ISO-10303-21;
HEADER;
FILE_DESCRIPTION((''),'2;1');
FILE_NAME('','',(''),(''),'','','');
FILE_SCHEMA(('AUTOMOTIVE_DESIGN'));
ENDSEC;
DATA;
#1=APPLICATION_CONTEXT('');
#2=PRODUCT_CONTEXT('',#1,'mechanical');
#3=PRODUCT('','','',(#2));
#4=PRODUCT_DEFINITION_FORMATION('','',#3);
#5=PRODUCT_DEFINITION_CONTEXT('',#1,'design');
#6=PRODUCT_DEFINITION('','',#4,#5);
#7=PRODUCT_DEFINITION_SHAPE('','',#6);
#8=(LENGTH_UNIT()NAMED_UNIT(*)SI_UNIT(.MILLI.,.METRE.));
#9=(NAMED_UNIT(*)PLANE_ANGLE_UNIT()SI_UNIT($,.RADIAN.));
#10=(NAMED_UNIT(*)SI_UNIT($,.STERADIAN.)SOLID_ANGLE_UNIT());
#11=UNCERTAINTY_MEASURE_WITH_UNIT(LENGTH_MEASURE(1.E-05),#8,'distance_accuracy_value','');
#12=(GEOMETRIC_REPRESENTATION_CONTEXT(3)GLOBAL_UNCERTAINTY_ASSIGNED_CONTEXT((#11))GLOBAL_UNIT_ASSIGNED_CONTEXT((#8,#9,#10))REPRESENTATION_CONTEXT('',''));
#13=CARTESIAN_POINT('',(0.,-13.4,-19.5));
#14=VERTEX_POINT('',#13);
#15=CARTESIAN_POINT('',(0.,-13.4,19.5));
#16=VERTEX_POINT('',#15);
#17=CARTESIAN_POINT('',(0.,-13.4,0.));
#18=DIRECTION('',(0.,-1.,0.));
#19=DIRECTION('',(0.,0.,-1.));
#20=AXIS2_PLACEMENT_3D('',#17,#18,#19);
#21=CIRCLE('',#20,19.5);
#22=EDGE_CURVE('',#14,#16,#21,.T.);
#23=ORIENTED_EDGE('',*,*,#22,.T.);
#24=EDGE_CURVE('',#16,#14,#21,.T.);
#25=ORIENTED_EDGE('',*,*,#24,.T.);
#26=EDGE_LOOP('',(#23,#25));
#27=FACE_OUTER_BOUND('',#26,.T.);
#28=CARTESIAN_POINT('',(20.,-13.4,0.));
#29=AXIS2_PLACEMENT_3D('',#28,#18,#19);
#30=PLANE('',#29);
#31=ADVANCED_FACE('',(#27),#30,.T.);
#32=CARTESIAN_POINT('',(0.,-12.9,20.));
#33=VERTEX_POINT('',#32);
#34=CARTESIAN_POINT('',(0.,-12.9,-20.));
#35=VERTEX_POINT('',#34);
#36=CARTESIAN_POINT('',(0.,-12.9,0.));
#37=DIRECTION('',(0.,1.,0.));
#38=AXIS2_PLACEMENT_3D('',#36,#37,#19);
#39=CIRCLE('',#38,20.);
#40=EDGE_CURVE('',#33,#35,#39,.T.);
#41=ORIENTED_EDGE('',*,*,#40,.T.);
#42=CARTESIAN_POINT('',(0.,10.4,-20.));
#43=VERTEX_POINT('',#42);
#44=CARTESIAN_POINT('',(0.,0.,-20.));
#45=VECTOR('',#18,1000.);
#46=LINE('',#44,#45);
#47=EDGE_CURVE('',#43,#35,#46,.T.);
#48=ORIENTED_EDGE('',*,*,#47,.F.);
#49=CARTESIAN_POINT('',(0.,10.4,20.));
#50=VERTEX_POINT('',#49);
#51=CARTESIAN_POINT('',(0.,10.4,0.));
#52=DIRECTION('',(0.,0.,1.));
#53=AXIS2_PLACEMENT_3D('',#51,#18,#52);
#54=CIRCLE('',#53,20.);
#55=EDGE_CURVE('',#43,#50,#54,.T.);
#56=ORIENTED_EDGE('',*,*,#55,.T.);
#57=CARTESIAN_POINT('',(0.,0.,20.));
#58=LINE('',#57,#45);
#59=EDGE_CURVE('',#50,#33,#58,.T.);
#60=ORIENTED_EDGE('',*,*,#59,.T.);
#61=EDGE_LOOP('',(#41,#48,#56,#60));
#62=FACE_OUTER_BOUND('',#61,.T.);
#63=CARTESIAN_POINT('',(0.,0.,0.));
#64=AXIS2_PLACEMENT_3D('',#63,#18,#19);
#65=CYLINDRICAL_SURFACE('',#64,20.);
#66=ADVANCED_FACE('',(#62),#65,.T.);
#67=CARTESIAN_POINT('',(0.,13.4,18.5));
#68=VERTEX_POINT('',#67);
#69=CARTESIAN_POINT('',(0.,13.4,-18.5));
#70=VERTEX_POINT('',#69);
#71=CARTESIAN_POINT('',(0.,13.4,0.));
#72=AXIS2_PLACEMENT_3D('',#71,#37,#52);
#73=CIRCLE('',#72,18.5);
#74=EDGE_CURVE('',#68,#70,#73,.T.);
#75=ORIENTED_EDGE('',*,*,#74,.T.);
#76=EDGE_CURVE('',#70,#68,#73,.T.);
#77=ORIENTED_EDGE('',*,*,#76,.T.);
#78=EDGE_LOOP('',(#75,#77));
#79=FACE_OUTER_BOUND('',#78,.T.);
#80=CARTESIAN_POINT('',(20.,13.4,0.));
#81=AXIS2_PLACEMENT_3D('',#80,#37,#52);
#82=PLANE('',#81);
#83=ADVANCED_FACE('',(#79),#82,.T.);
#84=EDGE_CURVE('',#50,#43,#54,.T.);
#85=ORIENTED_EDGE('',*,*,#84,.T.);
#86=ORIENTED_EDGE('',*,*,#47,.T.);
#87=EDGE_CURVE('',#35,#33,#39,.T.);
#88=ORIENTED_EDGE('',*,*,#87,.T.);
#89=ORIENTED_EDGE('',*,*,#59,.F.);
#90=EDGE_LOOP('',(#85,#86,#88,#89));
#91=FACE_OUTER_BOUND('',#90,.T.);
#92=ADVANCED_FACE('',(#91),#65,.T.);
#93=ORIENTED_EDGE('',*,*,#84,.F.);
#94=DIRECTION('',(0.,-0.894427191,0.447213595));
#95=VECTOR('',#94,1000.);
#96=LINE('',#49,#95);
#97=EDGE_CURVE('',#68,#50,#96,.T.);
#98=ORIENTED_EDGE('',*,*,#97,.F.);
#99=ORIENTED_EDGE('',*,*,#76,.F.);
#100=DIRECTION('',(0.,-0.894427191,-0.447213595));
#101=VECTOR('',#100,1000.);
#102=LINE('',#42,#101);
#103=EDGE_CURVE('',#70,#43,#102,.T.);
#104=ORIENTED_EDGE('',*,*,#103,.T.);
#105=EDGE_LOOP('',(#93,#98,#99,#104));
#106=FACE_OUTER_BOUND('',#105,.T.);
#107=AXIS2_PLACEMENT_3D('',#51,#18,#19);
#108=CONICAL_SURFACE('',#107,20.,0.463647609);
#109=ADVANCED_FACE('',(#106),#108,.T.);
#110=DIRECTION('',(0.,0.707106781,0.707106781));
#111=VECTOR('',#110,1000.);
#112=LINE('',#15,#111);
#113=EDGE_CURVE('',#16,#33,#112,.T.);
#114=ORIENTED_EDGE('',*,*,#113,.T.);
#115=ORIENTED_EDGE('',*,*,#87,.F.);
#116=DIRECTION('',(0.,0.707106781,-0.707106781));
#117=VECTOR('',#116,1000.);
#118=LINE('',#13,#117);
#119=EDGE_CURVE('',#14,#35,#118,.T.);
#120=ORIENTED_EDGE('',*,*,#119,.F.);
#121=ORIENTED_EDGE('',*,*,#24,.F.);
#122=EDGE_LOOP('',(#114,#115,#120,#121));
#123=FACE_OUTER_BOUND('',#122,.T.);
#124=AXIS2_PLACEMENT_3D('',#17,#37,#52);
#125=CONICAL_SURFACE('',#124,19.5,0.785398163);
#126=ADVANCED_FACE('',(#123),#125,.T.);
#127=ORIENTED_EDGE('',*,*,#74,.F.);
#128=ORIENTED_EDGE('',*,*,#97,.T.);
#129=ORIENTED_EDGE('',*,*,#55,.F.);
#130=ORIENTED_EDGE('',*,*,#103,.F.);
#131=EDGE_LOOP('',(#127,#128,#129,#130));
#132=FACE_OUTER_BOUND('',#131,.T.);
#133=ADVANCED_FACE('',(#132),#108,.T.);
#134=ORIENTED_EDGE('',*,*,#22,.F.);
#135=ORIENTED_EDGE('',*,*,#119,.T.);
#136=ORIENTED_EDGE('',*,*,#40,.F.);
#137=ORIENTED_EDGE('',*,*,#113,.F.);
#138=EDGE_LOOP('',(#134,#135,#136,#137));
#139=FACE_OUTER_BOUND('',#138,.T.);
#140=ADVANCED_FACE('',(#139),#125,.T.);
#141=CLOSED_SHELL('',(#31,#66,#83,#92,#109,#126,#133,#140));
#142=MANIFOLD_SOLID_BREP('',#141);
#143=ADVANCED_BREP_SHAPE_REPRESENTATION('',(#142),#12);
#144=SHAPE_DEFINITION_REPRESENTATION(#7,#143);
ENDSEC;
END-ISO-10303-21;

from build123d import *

# Parameters (mm, degrees)
SKETCH1_W      = 20
SKETCH1_H      = 26.8
CHAMFER1_SIZE  = 1.5
CHAMFER1_SIZE2 = 3
CHAMFER2_SIZE  = 0.5


with BuildPart() as part:
    # Sketch1 → Revolve1 (revolve)
    with BuildSketch(Plane.XY, mode=Mode.PRIVATE) as revolve1_sk:
        with Locations((10, 0)):
            Rectangle(SKETCH1_W, SKETCH1_H)
    revolve(revolve1_sk.sketch.rotate(Axis((0, 0, 0), (0, 1, 0)), 90), axis=Axis((0, 0, 0), (0, 1, 0)))

    # Chamfer1
    chamfer1_edges = [part.edges().sort_by_distance(p)[0] for p in [
        (0, 13.4, 20),
    ]]
    chamfer1_side = [part.faces().sort_by_distance(p)[0] for p in [
        (0, 13.4, 0),
    ]]
    chamfer(chamfer1_edges, length=CHAMFER1_SIZE, length2=CHAMFER1_SIZE2, reference=chamfer1_side[0])

    # Chamfer2
    chamfer2_edges = [part.edges().sort_by_distance(p)[0] for p in [
        (0, -13.4, 20),
    ]]
    chamfer(chamfer2_edges, length=CHAMFER2_SIZE)


solid = part.part
